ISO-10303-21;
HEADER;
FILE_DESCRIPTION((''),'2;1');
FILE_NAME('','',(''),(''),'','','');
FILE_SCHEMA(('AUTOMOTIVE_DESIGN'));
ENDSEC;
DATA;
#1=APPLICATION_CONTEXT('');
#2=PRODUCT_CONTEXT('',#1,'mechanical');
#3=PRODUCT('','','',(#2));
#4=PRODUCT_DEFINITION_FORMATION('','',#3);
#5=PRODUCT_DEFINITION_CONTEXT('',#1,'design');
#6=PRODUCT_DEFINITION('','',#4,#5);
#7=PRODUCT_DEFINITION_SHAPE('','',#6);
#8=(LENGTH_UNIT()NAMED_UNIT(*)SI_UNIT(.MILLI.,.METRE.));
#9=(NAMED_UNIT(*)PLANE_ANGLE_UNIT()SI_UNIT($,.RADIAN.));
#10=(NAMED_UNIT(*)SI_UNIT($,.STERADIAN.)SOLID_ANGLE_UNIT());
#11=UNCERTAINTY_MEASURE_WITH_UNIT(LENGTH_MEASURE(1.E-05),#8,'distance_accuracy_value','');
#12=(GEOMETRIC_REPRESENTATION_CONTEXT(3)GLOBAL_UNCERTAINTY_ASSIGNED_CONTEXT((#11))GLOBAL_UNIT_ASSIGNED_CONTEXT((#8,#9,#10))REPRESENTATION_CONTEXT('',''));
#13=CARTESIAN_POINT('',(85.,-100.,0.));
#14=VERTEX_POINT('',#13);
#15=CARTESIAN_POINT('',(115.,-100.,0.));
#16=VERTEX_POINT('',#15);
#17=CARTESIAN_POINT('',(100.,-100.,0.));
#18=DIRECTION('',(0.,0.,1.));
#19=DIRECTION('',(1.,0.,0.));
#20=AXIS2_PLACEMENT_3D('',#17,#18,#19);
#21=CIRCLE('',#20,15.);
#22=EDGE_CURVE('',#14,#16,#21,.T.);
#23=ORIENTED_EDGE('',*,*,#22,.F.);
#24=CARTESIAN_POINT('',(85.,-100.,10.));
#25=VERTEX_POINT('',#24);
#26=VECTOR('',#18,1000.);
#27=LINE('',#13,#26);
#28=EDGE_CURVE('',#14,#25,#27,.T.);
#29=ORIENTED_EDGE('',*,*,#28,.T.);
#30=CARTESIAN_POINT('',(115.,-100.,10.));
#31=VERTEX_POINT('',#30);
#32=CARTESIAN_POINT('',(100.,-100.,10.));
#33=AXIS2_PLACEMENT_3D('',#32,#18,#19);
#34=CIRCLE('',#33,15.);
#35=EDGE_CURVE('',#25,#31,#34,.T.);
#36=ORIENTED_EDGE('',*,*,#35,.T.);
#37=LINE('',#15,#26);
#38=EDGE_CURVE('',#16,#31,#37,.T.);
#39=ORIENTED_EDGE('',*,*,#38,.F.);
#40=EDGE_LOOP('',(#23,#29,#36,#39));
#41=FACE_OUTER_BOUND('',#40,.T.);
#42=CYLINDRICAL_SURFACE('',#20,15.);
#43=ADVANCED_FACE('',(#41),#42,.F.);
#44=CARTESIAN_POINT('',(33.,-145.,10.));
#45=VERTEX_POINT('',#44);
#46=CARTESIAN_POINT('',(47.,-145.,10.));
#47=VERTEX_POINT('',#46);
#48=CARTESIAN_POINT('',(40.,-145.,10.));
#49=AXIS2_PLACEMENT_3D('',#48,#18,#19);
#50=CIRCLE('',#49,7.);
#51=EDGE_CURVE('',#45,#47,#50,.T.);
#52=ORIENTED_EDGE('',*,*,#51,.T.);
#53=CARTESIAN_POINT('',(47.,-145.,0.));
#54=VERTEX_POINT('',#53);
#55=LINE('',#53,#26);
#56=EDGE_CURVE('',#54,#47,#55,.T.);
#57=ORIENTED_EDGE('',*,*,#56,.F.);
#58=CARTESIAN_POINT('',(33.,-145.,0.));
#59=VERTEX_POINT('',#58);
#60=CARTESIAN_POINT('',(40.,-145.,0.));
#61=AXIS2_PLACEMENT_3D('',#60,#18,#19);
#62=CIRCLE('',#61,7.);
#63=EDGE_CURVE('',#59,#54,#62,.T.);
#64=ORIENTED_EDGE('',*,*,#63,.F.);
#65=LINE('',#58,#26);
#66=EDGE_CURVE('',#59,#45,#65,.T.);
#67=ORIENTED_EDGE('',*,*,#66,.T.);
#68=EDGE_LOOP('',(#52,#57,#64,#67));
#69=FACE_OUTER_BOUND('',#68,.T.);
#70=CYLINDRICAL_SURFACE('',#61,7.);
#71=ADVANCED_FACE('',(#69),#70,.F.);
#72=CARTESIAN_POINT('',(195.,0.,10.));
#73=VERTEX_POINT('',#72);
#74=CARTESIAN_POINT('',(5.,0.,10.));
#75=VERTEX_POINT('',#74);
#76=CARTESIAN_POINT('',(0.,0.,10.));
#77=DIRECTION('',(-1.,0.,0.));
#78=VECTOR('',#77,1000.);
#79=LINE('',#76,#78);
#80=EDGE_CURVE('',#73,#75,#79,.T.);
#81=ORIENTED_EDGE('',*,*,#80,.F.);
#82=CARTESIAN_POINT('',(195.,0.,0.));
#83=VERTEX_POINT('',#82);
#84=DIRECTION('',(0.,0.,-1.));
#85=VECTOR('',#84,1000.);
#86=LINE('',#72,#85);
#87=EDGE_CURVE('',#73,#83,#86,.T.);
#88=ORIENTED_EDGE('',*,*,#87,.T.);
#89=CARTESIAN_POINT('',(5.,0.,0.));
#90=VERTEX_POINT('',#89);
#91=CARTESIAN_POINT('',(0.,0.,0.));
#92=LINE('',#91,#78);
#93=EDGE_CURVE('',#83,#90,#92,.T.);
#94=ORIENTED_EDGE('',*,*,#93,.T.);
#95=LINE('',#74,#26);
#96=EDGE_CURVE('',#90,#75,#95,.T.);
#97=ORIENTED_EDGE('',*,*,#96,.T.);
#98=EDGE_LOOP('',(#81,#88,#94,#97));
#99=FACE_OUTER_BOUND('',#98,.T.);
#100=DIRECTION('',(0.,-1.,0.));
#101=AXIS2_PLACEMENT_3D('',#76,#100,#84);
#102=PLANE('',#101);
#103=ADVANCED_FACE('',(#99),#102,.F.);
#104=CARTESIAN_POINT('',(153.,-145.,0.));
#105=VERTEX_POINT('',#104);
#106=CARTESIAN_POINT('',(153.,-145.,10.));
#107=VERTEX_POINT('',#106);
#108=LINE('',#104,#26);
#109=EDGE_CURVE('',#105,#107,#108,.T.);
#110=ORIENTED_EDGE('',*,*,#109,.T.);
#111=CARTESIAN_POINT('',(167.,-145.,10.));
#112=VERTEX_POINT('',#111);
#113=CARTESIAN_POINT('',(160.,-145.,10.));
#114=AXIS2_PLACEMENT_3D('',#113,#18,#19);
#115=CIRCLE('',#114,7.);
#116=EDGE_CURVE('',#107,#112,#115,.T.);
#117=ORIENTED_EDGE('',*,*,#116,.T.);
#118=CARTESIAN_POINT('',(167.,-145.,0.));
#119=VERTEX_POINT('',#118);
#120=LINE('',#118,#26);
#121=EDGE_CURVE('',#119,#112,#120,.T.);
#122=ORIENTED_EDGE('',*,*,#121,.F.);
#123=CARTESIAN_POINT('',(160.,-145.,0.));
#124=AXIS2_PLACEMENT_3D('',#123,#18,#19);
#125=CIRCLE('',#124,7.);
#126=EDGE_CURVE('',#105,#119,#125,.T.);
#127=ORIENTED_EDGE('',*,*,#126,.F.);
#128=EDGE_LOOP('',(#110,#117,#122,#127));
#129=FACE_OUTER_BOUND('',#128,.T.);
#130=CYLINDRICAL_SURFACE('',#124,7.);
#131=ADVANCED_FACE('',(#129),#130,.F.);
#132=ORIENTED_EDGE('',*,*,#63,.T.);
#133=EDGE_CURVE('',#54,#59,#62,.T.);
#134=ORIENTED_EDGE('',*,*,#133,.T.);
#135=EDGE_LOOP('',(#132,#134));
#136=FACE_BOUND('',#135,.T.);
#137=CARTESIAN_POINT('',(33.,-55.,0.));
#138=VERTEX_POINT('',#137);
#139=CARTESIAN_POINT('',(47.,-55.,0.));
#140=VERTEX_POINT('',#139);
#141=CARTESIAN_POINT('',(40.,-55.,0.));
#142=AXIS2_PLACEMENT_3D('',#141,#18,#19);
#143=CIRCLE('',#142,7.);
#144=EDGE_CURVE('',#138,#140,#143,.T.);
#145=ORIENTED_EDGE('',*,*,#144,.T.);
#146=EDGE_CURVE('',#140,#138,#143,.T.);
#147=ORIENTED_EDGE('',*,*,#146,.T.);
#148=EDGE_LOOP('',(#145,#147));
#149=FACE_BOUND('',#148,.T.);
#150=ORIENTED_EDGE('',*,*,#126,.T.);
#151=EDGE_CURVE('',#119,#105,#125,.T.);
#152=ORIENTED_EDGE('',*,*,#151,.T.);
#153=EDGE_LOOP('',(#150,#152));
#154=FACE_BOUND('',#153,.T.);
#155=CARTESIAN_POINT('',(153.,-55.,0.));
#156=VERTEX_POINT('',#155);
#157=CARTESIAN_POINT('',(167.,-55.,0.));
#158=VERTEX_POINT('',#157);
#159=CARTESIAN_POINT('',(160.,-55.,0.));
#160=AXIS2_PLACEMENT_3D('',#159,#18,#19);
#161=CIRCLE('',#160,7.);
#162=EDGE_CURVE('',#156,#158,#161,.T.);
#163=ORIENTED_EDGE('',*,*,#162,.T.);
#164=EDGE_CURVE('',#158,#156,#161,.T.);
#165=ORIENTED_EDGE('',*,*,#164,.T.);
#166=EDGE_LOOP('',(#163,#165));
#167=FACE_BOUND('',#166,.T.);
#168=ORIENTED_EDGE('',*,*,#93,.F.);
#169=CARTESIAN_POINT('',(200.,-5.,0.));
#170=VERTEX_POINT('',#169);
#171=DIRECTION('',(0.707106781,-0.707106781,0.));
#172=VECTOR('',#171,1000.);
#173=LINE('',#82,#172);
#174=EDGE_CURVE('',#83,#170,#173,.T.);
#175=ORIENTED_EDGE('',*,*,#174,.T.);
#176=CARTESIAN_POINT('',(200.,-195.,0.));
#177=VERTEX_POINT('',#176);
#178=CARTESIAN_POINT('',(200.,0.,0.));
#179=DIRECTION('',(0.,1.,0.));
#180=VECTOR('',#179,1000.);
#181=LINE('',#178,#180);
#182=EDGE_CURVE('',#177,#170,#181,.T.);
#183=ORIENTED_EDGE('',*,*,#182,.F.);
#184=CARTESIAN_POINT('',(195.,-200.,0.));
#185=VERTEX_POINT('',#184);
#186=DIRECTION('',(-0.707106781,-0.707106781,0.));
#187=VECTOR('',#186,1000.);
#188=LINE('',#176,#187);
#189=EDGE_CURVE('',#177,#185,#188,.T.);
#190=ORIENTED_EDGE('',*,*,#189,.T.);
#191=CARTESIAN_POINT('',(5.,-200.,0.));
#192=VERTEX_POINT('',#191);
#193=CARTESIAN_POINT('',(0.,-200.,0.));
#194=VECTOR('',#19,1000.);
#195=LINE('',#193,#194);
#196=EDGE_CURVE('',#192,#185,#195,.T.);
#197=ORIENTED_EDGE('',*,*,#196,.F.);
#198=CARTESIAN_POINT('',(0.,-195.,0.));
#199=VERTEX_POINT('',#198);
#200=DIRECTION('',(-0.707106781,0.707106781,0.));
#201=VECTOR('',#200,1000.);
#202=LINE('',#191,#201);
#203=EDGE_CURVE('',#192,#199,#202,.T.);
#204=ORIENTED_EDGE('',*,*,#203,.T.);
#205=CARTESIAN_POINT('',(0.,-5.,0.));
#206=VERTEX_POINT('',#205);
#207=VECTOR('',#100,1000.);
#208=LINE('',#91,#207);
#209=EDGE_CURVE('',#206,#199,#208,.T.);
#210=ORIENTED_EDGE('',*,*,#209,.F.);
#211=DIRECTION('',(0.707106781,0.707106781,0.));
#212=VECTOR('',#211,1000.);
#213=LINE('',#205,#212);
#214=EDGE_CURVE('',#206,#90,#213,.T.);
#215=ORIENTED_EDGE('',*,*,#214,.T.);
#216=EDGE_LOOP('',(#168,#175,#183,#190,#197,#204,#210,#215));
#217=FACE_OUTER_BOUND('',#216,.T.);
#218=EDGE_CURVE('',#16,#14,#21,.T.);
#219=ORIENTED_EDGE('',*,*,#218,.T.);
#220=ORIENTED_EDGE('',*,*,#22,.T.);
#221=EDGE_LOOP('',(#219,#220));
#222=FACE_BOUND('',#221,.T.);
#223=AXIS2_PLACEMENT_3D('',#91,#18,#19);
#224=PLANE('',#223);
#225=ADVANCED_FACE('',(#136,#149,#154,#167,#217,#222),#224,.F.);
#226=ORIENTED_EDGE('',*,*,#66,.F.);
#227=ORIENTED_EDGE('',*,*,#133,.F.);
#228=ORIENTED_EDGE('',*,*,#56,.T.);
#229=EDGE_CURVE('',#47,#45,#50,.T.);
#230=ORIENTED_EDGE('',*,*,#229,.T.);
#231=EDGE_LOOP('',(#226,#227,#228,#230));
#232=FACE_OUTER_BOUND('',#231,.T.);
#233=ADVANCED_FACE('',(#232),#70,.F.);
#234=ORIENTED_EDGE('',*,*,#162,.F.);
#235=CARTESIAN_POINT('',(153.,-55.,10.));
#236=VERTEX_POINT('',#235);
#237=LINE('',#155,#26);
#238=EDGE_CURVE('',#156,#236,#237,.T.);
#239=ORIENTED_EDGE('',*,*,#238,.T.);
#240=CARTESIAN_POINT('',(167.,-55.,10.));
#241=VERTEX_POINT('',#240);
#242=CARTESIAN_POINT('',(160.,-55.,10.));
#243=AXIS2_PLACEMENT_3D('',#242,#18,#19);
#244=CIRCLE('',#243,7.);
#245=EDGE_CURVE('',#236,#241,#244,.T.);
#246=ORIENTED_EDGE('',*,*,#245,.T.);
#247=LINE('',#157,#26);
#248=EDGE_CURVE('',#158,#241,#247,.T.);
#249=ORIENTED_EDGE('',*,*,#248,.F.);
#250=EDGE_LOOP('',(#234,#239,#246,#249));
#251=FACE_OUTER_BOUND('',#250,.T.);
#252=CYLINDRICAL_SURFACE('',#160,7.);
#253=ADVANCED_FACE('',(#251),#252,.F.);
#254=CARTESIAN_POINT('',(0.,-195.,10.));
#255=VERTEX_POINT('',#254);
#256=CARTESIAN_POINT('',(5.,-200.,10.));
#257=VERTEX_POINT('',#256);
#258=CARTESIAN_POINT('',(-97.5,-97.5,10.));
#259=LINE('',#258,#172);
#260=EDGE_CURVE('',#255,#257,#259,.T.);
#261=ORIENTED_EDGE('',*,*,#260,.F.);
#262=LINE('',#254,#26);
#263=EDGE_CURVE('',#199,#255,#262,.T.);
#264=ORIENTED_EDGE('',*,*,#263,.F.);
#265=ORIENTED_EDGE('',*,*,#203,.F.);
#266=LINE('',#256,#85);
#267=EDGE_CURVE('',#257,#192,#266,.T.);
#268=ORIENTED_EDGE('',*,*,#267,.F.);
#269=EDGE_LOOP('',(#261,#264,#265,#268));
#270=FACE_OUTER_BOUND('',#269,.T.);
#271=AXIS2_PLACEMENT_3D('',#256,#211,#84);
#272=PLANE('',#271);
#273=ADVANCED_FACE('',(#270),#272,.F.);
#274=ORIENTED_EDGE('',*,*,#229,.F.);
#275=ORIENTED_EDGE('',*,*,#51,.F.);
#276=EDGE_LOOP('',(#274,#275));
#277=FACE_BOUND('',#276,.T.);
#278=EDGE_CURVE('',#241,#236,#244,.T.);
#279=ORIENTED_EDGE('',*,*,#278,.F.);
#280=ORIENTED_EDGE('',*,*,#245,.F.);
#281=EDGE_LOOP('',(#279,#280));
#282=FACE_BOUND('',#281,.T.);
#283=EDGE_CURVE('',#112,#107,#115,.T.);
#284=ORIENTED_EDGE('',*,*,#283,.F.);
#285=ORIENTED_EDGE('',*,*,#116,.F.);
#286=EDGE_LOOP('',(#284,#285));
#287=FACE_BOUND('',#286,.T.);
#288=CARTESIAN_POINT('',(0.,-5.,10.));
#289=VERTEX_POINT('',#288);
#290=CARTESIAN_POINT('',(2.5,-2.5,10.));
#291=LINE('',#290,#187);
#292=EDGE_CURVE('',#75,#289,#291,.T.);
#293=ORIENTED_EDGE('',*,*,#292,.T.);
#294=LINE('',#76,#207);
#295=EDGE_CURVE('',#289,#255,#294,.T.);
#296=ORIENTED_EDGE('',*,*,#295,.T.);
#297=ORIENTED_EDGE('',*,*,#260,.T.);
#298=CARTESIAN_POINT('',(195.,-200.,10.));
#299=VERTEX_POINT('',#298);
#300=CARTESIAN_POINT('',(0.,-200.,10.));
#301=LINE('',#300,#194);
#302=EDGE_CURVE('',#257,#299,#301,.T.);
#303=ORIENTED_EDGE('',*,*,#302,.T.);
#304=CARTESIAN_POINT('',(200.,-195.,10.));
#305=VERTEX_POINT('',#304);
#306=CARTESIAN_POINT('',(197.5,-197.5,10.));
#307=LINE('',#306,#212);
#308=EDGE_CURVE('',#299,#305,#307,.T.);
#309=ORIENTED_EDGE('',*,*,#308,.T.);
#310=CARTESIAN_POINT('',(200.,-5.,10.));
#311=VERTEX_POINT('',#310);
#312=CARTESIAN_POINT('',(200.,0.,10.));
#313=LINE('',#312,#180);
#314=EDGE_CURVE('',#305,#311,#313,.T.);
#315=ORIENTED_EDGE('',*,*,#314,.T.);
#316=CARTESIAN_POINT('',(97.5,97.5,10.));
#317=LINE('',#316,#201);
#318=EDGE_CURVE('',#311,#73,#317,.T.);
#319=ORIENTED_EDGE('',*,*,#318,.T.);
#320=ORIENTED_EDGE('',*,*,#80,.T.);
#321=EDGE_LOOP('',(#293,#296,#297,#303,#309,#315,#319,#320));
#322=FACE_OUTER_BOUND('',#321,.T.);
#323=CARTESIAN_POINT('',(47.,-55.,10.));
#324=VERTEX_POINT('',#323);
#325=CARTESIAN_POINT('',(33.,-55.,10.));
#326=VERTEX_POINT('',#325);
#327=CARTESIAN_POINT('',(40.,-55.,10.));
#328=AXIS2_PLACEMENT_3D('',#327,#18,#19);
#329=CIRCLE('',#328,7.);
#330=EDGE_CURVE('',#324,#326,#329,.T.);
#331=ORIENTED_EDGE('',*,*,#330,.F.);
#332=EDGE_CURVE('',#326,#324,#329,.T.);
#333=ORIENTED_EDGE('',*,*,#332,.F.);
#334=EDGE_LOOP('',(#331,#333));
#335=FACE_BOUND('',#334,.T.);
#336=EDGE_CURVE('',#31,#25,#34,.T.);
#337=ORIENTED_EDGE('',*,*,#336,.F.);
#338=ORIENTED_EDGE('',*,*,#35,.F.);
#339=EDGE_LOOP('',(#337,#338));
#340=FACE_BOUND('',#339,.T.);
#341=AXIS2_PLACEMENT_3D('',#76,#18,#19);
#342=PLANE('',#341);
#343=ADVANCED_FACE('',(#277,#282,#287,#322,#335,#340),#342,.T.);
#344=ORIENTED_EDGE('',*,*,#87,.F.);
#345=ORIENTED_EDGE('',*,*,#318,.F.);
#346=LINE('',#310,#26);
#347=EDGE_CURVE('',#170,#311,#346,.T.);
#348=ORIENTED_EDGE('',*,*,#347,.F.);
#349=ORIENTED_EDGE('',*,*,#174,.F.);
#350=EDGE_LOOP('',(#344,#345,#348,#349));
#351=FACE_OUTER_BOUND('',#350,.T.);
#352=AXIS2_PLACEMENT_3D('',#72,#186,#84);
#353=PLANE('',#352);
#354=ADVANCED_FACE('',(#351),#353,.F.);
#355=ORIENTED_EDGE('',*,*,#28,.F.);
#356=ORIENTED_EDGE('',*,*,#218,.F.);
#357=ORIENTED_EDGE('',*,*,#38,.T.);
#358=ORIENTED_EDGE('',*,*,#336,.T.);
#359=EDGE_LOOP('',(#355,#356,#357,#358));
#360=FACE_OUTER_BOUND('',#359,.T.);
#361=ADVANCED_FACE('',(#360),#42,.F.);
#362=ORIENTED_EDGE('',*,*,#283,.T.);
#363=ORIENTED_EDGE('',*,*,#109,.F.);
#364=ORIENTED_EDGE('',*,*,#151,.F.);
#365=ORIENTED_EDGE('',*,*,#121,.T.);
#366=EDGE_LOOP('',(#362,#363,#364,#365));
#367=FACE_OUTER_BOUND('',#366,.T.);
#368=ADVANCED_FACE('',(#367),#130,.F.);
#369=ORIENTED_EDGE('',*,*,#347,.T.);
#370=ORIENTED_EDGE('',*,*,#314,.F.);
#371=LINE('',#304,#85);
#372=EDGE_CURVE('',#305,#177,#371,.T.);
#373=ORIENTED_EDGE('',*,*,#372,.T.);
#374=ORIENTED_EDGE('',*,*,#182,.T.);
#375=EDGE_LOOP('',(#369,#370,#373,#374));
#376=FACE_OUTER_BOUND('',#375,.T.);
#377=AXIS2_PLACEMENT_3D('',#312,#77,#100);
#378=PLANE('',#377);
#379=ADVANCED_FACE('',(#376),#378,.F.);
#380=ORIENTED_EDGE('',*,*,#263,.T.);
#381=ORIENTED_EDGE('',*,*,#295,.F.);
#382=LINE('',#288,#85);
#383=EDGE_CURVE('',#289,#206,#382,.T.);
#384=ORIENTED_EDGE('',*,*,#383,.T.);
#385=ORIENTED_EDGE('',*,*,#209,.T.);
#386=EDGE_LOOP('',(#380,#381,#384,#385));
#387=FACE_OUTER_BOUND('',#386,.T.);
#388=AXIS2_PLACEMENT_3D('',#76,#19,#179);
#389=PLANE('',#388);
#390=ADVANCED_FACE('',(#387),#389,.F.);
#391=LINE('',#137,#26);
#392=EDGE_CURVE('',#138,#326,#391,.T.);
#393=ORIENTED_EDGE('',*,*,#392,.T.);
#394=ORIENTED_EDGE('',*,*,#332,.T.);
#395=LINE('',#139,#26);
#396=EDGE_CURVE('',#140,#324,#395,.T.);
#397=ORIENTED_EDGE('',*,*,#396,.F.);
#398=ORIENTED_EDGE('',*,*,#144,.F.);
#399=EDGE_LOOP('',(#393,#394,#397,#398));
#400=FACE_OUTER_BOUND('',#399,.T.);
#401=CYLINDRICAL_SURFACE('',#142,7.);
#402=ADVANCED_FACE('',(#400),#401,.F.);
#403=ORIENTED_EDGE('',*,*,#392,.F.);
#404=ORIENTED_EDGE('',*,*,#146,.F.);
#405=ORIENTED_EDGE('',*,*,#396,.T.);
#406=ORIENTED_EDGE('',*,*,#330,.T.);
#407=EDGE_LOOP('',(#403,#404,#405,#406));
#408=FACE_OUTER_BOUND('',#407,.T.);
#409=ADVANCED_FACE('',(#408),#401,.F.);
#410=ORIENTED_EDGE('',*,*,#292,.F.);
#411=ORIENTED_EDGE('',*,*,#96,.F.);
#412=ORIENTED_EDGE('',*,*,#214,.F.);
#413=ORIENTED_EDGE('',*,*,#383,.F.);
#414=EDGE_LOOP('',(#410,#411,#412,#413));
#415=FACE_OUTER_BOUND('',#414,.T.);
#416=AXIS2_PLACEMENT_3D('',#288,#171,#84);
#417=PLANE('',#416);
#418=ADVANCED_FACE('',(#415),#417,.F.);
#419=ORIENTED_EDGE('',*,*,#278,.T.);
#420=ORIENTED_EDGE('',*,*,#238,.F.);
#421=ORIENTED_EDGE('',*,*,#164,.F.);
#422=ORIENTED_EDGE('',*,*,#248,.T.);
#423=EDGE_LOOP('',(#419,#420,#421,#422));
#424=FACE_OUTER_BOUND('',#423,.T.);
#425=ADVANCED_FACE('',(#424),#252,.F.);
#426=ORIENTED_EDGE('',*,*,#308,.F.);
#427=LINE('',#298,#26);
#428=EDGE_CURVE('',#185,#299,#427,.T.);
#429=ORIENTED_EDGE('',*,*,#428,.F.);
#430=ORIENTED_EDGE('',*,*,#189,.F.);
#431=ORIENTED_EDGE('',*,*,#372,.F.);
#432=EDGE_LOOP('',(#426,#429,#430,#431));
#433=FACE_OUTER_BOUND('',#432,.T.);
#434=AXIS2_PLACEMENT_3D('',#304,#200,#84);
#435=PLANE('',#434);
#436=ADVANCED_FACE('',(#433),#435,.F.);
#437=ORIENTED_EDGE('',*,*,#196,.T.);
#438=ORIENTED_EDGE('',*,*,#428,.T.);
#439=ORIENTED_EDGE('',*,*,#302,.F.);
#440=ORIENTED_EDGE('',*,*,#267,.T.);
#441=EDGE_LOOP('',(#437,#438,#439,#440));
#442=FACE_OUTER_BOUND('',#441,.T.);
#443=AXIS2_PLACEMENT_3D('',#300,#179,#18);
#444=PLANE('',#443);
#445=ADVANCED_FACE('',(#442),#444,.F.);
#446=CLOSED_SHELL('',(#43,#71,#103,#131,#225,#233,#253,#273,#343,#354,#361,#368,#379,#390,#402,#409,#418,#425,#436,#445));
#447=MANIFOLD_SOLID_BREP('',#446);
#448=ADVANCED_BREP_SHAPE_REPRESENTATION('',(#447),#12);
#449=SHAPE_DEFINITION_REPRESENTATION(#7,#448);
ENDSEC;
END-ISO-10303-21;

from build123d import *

# Parameters (mm, degrees)
SKETCH_1_W          = 200
SKETCH_1_H          = 200
EXTRUDE_1_DEPTH     = 10
SKETCH_2_R          = 7
SKETCH_2_R_2        = 15
CUT_EXTRUDE_1_DEPTH = 284.019433962
CHAMFER_1_SIZE      = 5


with BuildPart() as part:
    # 草图1 → 凸台-拉伸1 (new body)
    with BuildSketch(Plane.XY):
        with Locations((100, -100)):
            Rectangle(SKETCH_1_W, SKETCH_1_H)
    extrude(amount=EXTRUDE_1_DEPTH)

    # 草图2 → 切除-拉伸1 (cut, through all)
    with BuildSketch(Plane.XY.offset(10)):
        with Locations((40, -55)):
            Circle(SKETCH_2_R)
        with Locations((40, -145)):
            Circle(SKETCH_2_R)
        with Locations((160, -145)):
            Circle(SKETCH_2_R)
        with Locations((160, -55)):
            Circle(SKETCH_2_R)
        with Locations((100, -100)):
            Circle(SKETCH_2_R_2)
    extrude(amount=-CUT_EXTRUDE_1_DEPTH, mode=Mode.SUBTRACT)

    # 倒角1
    chamfer_1_edges = [part.edges().sort_by_distance(p)[0] for p in [
        (0, 0, 5),
        (200, 0, 5),
        (200, -200, 5),
        (0, -200, 5),
    ]]
    chamfer(chamfer_1_edges, length=CHAMFER_1_SIZE)


solid = part.part
